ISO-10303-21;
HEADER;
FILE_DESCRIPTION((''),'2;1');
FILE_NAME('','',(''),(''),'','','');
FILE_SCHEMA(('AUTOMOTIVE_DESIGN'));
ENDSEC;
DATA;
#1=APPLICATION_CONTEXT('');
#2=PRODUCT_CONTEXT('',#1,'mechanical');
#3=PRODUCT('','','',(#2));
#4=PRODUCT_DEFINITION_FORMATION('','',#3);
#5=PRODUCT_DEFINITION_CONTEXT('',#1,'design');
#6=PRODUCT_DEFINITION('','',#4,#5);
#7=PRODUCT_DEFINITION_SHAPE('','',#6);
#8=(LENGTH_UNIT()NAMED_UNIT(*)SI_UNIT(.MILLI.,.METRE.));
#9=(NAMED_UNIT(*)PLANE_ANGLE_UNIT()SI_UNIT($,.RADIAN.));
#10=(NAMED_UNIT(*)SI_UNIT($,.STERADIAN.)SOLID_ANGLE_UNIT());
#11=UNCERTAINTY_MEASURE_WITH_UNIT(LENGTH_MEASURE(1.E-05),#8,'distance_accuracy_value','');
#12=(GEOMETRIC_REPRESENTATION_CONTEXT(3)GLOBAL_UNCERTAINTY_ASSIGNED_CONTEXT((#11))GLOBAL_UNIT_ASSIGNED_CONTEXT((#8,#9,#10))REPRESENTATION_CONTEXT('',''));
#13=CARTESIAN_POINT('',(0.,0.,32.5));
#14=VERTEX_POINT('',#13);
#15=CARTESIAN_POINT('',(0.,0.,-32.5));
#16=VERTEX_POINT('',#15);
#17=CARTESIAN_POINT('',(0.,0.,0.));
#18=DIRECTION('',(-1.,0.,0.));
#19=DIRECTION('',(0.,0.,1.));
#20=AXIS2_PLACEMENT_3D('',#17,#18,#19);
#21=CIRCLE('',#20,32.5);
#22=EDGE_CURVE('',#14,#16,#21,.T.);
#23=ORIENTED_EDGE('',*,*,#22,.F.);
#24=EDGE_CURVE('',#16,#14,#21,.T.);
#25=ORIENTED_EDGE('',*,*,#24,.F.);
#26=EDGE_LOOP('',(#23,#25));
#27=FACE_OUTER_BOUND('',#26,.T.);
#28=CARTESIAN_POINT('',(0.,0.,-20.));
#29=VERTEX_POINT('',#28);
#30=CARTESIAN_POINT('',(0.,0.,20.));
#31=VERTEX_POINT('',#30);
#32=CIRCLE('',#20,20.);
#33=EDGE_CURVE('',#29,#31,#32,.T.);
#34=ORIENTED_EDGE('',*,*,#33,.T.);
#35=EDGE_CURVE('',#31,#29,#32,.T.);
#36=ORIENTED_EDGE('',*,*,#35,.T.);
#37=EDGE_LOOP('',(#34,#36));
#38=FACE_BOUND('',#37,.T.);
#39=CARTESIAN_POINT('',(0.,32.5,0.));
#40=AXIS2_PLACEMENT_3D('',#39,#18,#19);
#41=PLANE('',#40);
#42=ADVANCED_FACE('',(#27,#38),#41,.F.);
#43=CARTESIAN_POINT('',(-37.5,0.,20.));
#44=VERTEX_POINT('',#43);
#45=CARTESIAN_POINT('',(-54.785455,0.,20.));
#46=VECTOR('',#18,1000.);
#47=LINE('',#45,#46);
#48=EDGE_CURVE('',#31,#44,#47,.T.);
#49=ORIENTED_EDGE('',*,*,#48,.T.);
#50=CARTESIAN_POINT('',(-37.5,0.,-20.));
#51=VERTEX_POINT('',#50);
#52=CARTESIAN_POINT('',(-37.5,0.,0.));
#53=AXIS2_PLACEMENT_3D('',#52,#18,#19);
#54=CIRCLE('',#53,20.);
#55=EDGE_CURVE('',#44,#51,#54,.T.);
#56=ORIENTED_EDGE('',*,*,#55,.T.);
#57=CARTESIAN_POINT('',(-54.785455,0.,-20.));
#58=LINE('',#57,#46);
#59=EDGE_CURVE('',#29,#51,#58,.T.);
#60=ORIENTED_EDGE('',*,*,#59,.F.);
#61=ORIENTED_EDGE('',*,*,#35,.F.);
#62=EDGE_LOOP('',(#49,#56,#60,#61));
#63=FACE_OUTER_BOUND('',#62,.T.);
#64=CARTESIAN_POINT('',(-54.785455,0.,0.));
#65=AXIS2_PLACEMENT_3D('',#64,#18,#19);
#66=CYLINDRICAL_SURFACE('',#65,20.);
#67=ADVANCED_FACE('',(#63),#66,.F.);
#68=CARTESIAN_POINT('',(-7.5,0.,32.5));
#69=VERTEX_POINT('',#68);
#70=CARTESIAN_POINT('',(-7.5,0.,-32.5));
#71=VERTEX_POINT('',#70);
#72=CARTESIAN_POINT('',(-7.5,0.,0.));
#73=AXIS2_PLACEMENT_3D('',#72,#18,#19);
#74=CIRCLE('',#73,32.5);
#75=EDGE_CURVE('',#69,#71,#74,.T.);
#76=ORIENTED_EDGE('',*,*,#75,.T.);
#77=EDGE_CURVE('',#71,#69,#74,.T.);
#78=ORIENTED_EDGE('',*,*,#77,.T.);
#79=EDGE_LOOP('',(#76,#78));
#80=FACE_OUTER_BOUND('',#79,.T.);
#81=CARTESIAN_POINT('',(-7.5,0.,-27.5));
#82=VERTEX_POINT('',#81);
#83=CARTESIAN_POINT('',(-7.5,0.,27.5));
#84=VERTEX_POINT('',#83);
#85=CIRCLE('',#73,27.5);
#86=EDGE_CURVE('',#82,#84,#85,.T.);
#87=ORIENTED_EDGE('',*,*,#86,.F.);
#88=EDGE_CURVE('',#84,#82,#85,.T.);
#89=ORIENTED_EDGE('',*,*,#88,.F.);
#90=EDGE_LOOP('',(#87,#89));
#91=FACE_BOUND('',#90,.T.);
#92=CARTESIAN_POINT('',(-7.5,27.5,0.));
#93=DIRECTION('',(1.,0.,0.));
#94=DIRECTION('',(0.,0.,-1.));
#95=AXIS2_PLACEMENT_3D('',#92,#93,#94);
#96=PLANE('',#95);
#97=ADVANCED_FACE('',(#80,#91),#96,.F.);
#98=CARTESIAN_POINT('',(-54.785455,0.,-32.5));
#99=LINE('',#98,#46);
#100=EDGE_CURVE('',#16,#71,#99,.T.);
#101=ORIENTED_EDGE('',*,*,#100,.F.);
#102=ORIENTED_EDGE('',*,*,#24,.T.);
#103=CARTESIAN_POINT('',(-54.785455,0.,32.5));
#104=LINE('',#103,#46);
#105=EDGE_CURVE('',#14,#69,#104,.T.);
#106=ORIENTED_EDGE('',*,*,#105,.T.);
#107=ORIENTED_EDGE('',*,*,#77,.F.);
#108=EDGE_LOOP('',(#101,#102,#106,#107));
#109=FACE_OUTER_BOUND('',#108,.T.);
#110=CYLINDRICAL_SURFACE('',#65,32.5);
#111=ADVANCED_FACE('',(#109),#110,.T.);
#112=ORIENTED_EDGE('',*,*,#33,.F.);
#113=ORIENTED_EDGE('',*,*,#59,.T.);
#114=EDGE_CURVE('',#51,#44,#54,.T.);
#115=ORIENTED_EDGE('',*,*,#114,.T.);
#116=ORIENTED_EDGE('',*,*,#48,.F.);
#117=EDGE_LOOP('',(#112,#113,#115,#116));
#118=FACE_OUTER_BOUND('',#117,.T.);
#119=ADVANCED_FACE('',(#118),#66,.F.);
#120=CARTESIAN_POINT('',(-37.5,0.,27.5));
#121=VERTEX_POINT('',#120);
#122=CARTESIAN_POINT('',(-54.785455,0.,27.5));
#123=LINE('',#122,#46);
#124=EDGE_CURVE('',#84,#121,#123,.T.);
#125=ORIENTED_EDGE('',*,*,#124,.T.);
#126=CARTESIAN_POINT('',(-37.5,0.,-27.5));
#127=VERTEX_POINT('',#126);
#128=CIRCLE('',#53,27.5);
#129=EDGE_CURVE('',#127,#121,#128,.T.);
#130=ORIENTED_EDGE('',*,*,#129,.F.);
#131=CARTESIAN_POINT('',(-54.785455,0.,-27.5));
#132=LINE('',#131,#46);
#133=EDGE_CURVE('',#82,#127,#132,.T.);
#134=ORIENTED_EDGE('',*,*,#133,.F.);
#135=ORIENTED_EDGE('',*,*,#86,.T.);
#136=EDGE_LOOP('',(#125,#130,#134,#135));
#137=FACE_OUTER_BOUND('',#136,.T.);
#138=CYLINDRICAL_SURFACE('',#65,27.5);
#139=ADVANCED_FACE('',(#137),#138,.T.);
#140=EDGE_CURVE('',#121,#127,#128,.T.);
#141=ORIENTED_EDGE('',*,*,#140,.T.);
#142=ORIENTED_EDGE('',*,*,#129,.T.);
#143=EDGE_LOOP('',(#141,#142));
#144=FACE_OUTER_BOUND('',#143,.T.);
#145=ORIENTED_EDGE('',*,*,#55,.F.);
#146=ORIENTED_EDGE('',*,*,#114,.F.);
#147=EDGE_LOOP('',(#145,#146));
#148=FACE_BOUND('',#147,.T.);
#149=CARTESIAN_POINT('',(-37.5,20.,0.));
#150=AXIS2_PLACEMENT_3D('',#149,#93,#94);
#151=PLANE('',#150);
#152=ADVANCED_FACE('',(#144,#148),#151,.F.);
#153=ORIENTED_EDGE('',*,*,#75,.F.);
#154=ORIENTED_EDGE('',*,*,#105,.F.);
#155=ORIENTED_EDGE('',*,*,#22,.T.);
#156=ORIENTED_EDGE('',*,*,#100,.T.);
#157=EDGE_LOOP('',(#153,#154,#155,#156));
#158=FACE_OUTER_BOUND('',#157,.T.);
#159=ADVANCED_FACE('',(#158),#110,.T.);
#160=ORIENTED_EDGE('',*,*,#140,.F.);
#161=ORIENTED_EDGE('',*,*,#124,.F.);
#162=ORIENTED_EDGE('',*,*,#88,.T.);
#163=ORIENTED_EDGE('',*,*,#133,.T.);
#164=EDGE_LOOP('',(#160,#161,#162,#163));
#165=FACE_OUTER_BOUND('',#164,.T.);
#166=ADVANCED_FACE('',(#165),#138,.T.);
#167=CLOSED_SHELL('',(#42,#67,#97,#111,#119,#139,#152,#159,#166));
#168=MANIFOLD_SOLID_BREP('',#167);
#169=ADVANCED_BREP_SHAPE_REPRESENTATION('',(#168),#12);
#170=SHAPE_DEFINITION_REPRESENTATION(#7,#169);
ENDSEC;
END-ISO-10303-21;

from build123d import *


with BuildPart() as part:
    # Sketch 1 → Revolve 1 (revolve)
    with BuildSketch(Plane.XY, mode=Mode.PRIVATE) as revolve_1_sk:
        Polygon((0, 32.5), (0, 20), (-37.5, 20), (-37.5, 27.5), (-7.5, 27.5), (-7.5, 32.5), align=None)
    revolve(revolve_1_sk.sketch.rotate(Axis((-54.785454848, 0, 0), (1, 0, 0)), 90), axis=Axis((-54.785454848, 0, 0), (1, 0, 0)))


solid = part.part
